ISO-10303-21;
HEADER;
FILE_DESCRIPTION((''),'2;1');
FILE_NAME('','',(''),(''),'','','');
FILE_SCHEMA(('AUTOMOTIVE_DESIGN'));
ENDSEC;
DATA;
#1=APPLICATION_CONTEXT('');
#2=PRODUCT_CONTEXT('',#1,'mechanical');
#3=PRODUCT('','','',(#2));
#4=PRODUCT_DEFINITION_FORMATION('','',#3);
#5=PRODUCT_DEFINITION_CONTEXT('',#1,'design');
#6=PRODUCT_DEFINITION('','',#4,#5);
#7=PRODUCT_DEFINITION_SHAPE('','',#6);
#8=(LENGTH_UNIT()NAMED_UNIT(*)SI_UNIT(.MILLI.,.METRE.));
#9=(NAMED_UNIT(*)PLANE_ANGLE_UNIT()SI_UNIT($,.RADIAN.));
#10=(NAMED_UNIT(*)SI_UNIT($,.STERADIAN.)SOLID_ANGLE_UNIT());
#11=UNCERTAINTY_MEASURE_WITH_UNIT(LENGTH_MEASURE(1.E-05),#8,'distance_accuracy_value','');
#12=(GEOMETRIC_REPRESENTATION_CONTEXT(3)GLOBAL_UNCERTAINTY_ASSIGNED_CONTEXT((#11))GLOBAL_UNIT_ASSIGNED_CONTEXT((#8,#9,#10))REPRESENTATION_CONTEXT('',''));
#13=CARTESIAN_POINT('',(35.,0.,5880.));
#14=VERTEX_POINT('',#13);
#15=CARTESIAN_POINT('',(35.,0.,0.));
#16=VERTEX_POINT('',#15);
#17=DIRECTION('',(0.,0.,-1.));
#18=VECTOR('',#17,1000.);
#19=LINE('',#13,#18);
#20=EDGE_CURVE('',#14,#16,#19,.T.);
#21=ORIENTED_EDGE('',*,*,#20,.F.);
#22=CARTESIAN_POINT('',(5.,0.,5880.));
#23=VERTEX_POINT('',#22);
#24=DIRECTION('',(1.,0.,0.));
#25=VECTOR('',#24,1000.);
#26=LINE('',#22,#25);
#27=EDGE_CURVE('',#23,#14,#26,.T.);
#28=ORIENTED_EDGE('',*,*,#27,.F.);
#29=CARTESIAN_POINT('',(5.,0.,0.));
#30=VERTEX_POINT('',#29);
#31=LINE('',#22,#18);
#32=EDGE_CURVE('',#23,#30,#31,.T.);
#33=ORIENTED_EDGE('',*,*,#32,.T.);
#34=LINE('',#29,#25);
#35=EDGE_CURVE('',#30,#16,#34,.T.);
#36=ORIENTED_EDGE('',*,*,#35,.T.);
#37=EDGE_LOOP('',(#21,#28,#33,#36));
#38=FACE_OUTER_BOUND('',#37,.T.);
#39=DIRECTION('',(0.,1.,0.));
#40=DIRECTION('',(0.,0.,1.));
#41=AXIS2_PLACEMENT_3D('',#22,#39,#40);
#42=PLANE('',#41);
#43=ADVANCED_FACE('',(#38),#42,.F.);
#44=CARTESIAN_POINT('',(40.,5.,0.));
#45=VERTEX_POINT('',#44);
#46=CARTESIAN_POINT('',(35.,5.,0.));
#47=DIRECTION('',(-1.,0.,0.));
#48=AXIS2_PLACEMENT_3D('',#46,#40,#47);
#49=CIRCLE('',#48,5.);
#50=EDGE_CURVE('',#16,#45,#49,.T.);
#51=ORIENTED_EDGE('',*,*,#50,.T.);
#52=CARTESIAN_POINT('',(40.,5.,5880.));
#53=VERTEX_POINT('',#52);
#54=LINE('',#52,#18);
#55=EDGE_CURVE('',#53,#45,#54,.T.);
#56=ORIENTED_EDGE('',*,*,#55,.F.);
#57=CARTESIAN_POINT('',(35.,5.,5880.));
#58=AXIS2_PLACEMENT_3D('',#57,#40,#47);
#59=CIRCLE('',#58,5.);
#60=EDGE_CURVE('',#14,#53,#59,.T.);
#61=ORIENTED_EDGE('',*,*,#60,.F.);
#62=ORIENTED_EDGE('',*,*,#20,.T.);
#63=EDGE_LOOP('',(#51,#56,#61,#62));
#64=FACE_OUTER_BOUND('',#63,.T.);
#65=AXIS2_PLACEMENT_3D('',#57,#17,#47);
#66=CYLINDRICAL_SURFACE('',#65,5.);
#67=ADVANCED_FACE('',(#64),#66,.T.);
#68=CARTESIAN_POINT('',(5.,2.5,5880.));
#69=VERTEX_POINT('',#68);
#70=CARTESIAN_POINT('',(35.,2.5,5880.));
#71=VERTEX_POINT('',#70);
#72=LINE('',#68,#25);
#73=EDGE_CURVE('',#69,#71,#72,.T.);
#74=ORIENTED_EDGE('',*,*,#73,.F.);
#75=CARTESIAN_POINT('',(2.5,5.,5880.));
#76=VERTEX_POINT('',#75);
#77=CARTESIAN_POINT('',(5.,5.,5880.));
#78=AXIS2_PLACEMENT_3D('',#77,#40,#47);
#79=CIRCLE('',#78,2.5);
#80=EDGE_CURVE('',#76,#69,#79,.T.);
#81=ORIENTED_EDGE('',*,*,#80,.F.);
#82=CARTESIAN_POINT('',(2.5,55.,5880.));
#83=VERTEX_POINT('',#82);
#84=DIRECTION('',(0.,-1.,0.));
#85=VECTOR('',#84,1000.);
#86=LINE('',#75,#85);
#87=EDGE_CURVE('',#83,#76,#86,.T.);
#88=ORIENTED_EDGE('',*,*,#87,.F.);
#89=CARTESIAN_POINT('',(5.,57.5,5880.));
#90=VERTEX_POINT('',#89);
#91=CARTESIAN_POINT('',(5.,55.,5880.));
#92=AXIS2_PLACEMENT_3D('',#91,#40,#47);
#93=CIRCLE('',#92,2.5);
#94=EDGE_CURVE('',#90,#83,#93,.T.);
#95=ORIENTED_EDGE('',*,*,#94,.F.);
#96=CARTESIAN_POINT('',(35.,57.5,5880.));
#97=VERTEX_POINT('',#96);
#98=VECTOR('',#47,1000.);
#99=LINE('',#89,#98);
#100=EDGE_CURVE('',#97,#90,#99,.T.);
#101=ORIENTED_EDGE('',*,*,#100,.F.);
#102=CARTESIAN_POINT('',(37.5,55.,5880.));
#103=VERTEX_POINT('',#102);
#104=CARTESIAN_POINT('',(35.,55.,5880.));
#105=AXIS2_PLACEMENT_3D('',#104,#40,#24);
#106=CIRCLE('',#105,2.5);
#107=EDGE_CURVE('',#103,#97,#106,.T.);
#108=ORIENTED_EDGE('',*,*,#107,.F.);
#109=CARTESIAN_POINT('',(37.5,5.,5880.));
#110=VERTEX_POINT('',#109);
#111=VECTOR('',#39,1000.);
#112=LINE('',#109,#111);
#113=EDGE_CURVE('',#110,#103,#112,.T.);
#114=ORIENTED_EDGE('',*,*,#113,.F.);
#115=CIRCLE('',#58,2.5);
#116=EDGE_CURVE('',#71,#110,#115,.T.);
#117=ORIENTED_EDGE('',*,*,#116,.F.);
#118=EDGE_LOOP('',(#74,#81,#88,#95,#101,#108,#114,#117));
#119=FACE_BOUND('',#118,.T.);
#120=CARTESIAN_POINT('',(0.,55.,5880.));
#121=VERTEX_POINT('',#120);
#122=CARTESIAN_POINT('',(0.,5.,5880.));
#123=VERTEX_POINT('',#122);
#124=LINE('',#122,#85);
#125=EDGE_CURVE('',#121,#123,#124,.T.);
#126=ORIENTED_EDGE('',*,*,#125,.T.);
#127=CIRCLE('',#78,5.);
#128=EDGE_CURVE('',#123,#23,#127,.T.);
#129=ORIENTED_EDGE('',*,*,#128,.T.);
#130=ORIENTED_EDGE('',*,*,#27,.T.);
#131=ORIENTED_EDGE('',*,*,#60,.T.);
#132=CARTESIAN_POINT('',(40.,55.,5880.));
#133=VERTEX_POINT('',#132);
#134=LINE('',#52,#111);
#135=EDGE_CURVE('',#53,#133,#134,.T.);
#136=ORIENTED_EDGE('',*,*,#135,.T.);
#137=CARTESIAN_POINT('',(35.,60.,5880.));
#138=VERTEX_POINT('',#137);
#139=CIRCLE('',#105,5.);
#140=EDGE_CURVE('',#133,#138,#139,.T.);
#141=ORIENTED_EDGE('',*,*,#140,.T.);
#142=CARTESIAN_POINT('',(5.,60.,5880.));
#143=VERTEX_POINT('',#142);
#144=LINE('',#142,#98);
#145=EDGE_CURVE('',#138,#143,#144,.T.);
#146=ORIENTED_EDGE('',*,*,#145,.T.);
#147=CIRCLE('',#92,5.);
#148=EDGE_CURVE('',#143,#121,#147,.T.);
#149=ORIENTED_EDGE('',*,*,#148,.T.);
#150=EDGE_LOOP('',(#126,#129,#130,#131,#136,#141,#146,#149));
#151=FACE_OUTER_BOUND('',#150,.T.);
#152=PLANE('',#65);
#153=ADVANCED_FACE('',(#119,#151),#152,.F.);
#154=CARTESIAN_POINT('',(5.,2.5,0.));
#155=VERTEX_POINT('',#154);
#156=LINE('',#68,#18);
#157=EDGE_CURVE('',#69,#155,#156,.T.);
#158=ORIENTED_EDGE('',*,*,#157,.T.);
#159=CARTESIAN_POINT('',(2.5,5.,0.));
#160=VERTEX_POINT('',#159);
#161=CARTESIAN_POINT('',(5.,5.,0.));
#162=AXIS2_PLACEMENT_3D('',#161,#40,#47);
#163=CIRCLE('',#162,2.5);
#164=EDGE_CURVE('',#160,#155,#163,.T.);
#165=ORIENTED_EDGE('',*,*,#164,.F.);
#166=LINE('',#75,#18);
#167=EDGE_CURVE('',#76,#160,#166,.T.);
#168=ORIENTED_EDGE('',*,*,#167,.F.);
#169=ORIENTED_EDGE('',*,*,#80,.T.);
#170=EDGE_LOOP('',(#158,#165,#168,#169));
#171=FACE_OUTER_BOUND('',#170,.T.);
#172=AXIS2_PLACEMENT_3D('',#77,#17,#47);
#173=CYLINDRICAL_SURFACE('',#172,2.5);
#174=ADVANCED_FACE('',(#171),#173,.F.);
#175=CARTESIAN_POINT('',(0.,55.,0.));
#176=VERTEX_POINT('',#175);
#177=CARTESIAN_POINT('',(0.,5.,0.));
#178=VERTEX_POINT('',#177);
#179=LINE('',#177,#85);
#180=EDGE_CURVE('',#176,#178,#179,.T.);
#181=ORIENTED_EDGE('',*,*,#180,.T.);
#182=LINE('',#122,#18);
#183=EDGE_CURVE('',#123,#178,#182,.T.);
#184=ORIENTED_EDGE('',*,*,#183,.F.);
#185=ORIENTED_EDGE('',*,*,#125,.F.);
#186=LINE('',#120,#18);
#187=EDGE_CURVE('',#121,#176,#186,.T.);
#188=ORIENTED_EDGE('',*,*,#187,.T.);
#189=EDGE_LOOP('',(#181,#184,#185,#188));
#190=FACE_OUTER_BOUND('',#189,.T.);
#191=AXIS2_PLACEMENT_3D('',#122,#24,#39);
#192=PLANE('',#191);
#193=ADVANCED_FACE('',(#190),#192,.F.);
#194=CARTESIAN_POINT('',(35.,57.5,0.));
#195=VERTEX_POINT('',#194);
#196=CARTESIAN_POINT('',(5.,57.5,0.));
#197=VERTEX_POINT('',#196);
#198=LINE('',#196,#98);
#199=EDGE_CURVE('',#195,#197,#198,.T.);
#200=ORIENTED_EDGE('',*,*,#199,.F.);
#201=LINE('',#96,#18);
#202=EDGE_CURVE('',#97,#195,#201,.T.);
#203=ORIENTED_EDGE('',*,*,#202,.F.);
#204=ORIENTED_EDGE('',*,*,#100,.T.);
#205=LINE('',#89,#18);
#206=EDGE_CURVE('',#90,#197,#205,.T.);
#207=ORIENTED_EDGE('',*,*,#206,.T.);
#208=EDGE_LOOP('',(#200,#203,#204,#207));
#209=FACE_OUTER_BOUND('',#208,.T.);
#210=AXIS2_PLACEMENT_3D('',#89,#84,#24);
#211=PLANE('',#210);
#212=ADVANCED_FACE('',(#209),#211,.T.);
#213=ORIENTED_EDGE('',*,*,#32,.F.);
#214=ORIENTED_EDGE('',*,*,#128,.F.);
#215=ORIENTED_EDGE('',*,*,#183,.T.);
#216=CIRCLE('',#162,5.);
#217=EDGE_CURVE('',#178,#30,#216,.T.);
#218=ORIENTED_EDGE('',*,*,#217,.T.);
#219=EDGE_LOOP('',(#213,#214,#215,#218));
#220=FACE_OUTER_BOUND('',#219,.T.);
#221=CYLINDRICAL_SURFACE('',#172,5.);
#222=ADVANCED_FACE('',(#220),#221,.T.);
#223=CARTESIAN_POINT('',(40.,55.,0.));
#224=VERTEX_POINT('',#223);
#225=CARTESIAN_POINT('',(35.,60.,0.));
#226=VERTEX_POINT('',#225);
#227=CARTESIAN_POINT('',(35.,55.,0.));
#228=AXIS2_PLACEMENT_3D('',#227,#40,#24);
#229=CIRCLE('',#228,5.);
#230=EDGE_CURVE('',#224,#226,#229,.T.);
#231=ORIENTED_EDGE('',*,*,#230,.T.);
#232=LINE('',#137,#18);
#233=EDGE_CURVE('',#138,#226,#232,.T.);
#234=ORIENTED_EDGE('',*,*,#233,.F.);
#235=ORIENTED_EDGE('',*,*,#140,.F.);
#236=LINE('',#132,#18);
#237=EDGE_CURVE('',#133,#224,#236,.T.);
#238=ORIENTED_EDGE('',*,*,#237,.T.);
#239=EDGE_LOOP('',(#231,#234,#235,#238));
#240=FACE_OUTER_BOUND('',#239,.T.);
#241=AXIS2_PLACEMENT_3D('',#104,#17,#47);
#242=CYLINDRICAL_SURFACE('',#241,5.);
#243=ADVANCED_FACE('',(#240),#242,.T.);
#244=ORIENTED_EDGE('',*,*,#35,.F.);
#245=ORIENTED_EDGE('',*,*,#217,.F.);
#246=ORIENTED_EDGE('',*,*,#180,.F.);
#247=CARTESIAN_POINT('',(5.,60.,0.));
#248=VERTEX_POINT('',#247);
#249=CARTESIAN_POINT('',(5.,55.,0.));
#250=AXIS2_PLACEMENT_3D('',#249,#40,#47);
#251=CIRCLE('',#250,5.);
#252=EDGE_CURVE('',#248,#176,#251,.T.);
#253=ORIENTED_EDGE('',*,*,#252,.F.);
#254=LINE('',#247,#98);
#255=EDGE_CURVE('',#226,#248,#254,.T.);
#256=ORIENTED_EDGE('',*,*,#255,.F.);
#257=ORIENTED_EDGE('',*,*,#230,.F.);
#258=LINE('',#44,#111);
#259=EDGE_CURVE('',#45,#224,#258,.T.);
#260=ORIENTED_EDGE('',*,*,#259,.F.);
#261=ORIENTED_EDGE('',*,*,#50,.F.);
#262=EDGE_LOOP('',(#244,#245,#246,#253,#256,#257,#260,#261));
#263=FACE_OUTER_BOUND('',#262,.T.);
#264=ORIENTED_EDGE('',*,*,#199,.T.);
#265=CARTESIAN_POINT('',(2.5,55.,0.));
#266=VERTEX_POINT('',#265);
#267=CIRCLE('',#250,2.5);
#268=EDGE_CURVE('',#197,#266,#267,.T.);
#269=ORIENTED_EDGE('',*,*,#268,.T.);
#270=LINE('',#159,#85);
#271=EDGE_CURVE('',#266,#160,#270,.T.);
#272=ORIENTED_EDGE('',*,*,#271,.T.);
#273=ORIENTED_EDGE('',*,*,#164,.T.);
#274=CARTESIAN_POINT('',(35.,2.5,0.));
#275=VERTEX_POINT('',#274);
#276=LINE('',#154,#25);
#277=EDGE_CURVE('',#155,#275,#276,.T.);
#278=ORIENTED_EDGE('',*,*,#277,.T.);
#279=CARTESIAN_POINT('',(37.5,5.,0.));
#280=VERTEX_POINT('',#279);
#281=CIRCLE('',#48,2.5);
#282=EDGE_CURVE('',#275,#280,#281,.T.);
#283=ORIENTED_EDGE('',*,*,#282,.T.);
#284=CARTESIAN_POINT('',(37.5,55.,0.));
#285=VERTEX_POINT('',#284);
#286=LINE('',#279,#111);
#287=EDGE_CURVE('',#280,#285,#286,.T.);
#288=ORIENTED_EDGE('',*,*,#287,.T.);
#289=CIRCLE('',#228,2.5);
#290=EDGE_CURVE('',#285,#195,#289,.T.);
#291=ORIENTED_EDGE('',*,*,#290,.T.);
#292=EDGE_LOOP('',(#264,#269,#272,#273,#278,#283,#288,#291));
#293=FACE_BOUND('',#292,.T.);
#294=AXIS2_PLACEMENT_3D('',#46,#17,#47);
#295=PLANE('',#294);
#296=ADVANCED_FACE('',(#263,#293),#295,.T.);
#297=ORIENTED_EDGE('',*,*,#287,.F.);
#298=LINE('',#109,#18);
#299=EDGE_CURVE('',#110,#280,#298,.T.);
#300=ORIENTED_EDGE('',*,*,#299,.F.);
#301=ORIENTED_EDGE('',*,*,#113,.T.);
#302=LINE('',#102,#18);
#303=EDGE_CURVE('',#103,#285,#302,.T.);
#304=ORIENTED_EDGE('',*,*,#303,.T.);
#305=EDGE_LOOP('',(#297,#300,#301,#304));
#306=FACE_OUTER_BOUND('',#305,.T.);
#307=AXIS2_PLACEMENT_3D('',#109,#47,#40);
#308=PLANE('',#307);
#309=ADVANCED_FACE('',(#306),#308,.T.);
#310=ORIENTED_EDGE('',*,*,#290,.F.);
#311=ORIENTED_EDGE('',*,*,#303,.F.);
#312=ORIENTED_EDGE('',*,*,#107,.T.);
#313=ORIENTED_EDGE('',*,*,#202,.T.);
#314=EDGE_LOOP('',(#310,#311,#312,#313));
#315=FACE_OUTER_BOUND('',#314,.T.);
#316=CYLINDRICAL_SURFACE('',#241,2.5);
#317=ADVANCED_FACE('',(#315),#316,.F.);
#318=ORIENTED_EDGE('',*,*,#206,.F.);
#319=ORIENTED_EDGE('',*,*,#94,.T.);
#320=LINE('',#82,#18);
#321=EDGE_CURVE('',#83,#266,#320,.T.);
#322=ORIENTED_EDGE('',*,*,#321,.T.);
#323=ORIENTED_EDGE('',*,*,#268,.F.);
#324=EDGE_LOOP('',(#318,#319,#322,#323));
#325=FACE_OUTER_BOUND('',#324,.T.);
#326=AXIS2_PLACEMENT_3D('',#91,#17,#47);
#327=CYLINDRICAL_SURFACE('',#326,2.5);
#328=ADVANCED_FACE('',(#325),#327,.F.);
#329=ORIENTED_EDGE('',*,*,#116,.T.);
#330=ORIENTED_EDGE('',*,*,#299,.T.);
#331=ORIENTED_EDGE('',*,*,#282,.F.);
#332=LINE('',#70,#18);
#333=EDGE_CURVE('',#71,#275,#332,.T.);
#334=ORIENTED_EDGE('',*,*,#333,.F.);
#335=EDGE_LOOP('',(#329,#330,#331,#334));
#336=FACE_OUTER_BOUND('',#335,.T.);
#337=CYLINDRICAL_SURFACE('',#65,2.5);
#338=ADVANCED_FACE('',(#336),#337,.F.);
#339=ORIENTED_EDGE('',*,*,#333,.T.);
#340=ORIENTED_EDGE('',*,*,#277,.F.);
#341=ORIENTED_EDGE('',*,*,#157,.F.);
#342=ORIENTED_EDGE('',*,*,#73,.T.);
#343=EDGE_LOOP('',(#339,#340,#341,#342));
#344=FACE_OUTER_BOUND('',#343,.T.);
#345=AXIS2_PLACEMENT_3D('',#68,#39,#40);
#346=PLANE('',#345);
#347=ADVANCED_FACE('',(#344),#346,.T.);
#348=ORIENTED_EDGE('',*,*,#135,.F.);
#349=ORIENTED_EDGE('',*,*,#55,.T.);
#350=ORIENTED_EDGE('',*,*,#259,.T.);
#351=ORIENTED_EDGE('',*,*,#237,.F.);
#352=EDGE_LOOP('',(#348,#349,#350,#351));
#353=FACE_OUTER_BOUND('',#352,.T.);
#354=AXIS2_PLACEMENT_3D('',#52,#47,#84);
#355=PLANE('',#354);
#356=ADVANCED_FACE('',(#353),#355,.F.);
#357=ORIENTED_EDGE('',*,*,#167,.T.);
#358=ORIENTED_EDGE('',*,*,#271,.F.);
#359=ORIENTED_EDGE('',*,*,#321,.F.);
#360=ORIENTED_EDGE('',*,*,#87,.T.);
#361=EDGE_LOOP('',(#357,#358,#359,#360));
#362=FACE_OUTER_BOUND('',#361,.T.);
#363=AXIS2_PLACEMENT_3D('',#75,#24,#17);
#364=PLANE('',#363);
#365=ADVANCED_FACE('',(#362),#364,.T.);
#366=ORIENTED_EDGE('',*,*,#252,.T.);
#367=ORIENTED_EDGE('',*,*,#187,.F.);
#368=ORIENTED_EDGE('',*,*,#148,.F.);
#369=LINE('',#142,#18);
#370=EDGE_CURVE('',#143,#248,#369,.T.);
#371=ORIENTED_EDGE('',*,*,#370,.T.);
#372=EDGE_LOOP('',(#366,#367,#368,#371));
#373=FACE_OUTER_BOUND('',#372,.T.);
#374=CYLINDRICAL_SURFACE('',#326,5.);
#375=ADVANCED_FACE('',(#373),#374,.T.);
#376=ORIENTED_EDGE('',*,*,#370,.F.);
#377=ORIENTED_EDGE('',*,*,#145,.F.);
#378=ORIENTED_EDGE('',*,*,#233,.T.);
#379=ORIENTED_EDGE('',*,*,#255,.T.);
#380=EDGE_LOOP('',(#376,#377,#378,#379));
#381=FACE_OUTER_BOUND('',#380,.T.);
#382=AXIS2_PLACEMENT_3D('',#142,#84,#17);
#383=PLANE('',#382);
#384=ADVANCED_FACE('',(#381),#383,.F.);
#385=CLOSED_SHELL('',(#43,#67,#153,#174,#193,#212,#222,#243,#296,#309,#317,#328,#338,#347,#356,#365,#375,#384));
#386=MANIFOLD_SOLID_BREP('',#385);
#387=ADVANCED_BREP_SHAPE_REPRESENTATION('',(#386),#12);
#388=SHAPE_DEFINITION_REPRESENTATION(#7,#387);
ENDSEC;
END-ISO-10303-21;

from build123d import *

# Parameters (mm, degrees)
BOSS_EXTRUDE1_DEPTH = 5880


with BuildPart() as part:
    # Sketch1 → Boss-Extrude1 (new body)
    with BuildSketch(Plane.XY):
        with BuildLine():
            Line((5, 0), (35, 0))
            ThreePointArc((35, 0), (38.535533906, 1.464466094), (40, 5))
            Line((40, 5), (40, 55))
            ThreePointArc((40, 55), (38.535533906, 58.535533906), (35, 60))
            Line((35, 60), (5, 60))
            ThreePointArc((5, 60), (1.464466094, 58.535533906), (0, 55))
            Line((0, 55), (0, 5))
            ThreePointArc((0, 5), (1.464466094, 1.464466094), (5, 0))
        make_face()
        with BuildLine():
            Line((5, 2.5), (35, 2.5))
            ThreePointArc((35, 2.5), (36.767766953, 3.232233047), (37.5, 5))
            Line((37.5, 5), (37.5, 55))
            ThreePointArc((37.5, 55), (36.767766953, 56.767766953), (35, 57.5))
            Line((35, 57.5), (5, 57.5))
            ThreePointArc((5, 57.5), (3.232233047, 56.767766953), (2.5, 55))
            Line((2.5, 55), (2.5, 5))
            ThreePointArc((2.5, 5), (3.232233047, 3.232233047), (5, 2.5))
        make_face(mode=Mode.SUBTRACT)
    extrude(amount=BOSS_EXTRUDE1_DEPTH)


solid = part.part
